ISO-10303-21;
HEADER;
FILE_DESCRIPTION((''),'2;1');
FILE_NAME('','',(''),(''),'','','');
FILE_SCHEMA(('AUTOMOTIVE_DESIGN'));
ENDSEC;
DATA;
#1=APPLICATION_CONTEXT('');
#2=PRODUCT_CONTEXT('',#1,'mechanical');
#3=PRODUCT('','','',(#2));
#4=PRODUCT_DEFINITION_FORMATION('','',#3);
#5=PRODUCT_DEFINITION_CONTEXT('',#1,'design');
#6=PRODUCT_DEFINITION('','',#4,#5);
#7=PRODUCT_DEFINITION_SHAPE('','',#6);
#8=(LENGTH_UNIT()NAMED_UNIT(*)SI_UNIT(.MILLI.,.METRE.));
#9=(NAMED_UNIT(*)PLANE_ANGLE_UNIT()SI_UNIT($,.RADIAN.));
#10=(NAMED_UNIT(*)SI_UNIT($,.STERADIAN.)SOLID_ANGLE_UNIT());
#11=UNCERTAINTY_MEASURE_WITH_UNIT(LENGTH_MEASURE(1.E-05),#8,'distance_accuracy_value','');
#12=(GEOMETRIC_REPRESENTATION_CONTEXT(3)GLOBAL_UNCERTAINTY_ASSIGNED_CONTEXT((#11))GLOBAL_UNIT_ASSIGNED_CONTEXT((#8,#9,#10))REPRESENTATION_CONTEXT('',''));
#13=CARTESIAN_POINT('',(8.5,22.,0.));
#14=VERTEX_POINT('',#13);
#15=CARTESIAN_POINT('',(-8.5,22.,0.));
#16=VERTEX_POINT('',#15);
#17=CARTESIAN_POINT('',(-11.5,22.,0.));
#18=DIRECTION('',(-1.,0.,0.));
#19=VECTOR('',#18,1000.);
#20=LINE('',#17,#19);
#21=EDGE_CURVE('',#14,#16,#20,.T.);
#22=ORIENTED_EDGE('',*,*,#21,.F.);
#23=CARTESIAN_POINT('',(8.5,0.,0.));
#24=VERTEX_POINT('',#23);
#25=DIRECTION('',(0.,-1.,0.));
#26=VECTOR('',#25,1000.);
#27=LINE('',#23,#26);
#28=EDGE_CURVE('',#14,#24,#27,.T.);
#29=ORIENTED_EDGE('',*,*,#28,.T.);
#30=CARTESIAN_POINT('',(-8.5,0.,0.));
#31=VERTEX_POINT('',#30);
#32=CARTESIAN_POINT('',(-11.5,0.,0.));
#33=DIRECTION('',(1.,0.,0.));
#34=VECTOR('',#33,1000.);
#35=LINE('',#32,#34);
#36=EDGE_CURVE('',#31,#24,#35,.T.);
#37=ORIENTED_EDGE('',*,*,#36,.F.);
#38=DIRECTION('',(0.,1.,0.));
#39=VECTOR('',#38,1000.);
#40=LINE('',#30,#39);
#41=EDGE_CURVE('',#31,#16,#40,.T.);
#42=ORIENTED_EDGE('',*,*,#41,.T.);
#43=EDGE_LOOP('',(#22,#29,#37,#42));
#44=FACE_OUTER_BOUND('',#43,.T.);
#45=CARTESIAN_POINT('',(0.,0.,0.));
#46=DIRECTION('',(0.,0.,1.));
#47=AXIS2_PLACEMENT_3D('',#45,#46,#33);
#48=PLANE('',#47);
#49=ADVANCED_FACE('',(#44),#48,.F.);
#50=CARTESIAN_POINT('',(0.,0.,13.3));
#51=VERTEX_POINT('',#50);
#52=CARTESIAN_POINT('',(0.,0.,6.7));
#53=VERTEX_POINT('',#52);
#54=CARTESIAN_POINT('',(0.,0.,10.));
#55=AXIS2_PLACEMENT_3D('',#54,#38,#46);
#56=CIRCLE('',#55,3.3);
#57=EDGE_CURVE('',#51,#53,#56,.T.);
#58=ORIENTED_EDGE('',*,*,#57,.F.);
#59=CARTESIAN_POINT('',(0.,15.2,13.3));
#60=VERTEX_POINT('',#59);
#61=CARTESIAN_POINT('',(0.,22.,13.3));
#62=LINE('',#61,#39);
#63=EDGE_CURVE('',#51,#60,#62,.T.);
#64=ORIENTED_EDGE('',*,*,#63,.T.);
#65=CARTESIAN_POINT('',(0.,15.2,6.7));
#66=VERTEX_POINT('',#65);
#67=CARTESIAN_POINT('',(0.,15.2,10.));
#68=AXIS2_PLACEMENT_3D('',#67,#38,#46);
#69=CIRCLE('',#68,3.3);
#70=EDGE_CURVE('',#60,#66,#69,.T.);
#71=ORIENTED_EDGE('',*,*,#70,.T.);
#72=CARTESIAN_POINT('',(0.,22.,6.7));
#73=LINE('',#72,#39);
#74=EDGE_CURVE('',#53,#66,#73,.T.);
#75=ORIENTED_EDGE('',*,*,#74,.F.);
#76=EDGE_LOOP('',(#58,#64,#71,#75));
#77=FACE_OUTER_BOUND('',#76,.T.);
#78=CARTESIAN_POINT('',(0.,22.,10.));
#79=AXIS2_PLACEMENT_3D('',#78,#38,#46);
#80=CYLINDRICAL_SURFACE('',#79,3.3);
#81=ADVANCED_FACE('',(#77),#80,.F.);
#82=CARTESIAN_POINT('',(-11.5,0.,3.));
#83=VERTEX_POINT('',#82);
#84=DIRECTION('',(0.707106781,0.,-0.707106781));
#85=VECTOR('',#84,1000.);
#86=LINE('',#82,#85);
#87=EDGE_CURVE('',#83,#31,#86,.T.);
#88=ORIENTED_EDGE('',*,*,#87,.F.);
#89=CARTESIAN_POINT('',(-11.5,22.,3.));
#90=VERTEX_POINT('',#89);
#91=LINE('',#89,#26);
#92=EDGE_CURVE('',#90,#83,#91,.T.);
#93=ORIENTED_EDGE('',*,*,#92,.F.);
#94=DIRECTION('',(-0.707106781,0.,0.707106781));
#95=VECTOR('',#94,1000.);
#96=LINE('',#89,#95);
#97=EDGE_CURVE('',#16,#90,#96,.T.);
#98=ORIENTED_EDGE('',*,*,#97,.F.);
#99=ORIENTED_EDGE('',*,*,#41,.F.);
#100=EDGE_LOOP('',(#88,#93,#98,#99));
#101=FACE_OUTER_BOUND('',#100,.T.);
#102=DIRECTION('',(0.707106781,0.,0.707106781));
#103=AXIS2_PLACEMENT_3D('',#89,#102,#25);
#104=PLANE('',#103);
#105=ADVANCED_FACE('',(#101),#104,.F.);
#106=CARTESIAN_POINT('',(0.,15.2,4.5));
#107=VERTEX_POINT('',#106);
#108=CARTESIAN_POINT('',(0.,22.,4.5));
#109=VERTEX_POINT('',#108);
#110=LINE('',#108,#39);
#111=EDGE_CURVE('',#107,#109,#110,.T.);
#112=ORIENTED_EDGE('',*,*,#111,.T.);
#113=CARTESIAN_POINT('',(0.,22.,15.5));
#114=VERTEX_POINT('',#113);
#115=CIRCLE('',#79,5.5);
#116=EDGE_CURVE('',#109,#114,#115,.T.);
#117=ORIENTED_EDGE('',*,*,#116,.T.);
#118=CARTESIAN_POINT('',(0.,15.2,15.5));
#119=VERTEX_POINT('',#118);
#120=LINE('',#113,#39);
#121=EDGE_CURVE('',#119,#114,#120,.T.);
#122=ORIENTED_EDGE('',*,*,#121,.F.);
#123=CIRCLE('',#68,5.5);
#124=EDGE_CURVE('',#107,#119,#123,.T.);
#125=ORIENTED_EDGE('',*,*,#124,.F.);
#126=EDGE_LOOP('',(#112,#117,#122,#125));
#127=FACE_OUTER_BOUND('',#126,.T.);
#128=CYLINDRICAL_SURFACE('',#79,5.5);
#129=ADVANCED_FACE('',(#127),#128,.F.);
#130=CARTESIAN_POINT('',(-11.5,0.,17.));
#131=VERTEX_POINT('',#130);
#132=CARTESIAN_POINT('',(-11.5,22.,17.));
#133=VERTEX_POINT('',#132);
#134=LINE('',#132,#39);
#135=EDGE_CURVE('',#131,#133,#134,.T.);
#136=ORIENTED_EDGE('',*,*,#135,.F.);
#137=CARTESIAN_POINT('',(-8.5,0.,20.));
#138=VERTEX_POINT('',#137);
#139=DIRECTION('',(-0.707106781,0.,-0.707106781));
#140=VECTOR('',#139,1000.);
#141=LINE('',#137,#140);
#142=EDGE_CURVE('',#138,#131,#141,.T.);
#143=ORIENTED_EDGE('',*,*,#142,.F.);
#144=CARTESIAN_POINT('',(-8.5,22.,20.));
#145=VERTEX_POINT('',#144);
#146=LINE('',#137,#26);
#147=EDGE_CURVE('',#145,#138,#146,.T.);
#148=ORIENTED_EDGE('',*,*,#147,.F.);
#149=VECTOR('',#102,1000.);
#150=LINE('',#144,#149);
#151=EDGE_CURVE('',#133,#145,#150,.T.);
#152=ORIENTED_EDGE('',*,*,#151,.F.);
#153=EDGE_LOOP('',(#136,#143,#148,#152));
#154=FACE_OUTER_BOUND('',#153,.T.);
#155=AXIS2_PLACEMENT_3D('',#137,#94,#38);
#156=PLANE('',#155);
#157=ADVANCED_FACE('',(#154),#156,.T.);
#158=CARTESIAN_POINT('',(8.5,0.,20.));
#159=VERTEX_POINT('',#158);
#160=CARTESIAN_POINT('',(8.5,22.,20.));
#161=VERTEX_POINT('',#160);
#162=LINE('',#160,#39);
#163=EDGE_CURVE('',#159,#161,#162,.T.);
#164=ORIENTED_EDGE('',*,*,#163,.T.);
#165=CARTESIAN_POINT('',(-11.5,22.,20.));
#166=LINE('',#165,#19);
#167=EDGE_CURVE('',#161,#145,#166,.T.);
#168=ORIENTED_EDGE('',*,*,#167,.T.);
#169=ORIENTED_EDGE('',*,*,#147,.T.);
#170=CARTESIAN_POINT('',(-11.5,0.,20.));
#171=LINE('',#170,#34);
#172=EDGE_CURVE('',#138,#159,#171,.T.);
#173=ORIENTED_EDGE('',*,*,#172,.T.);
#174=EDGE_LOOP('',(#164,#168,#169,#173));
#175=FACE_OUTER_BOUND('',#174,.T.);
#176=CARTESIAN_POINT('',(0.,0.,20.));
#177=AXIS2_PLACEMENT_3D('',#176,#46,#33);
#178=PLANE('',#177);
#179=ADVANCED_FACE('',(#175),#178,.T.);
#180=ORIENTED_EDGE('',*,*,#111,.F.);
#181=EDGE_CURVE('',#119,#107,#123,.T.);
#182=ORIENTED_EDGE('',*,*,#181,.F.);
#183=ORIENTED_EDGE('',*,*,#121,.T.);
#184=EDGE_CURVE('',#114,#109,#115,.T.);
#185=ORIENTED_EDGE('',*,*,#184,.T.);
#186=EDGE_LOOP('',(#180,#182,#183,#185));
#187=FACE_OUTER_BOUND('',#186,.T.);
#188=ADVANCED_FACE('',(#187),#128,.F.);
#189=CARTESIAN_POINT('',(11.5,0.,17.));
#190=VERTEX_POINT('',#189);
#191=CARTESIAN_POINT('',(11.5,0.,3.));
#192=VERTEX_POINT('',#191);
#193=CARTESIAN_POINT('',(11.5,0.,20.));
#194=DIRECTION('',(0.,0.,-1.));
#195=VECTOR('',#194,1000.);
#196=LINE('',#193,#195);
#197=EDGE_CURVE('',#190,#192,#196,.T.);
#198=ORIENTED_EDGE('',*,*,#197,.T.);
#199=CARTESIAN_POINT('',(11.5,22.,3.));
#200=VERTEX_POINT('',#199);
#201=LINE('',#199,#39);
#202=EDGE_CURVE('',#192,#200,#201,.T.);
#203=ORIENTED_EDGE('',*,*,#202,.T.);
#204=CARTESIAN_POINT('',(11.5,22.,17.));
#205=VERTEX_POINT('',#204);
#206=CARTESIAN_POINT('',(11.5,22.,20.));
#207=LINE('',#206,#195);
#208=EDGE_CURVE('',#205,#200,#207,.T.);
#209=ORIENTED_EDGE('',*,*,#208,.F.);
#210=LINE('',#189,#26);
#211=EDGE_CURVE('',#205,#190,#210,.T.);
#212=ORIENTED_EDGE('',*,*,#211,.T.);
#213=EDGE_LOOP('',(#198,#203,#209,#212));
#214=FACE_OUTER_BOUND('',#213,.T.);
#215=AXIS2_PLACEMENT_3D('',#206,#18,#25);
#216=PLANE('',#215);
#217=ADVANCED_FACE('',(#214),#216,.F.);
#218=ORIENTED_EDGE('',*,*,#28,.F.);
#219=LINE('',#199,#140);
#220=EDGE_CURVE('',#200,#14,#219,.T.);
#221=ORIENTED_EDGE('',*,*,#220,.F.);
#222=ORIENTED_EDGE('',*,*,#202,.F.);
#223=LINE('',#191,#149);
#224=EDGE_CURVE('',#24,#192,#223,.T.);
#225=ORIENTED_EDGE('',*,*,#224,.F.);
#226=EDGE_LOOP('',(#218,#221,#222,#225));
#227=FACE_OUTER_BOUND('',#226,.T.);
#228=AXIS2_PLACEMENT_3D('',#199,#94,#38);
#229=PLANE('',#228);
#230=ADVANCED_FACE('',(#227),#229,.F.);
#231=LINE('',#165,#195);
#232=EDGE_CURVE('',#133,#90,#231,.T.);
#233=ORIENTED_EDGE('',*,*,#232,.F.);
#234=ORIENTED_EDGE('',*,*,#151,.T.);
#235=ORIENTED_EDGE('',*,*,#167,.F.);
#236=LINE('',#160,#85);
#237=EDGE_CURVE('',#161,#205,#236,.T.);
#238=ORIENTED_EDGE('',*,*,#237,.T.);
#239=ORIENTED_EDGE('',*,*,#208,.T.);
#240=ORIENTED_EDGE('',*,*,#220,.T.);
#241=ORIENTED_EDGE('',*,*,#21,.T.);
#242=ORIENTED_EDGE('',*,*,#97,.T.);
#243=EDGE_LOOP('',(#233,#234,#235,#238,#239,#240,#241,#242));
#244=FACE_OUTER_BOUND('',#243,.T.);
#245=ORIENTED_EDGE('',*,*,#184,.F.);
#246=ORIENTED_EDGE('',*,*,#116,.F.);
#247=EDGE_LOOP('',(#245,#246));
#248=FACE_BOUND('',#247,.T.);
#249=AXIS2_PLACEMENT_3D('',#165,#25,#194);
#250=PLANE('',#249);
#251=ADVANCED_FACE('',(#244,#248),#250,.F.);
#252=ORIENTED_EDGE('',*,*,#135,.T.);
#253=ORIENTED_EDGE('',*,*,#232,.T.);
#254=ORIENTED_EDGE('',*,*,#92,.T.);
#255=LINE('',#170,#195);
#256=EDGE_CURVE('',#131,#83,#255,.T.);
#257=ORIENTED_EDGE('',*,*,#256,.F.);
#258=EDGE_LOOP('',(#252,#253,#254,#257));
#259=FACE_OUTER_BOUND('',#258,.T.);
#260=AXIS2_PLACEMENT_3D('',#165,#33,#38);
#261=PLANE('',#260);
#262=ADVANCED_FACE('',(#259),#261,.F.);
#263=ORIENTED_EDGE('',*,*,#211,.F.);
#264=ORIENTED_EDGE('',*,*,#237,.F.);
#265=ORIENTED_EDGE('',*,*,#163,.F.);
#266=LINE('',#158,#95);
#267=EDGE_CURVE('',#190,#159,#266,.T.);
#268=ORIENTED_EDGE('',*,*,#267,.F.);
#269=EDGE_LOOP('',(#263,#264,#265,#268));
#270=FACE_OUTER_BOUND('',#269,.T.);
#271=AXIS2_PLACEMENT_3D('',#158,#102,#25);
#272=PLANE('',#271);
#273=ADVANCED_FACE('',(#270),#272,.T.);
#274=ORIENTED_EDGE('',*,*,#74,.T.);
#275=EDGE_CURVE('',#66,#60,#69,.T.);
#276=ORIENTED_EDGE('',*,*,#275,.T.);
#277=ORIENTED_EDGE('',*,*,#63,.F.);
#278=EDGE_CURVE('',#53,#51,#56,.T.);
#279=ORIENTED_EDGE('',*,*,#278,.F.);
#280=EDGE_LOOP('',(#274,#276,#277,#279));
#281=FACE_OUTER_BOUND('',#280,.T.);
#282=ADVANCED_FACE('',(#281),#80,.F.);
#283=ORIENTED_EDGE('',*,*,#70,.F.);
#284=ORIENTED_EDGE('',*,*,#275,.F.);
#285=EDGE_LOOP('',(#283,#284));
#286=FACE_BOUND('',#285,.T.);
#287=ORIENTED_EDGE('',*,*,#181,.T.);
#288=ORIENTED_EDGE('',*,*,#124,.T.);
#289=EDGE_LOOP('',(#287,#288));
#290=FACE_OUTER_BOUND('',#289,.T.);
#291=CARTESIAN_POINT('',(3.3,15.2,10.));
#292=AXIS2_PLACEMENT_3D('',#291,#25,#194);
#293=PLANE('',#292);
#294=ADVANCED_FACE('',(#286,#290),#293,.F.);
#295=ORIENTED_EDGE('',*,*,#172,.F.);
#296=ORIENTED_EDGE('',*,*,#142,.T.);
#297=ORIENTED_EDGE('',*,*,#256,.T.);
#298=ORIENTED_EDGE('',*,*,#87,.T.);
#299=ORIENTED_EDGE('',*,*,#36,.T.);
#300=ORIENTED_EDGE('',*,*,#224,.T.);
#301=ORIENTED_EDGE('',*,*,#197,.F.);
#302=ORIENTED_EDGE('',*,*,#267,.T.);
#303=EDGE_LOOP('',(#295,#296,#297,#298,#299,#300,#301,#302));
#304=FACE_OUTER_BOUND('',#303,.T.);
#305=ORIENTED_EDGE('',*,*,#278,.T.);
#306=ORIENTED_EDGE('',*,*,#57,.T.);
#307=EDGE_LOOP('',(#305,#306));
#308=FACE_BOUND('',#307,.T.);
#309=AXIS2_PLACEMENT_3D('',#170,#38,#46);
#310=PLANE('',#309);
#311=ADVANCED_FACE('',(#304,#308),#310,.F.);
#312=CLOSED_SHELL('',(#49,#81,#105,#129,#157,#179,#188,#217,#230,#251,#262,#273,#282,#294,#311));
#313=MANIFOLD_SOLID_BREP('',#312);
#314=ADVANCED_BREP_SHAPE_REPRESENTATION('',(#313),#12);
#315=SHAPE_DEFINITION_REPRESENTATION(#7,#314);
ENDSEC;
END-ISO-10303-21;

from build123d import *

# Parameters (mm, degrees)
SKETCH_1_W                = 23
SKETCH_1_H                = 22
EXTRUDE_1_DEPTH           = 20
HOLE_WIZARD_1_D           = 6.6
HOLE_WIZARD_1_CBORE_D     = 11
HOLE_WIZARD_1_CBORE_DEPTH = 6.8
CHAMFER_1_SIZE            = 3


with BuildPart() as part:
    # 草图1 → 凸台-拉伸1 (new body)
    with BuildSketch(Plane.XY):
        with Locations((0, 11)):
            Rectangle(SKETCH_1_W, SKETCH_1_H)
    extrude(amount=EXTRUDE_1_DEPTH)

    # 打孔尺寸(%根据)内六角圆柱头螺钉的类型1 (through all)
    with Locations(Plane(origin=(0, 22, 0), x_dir=(1, 0, 0), z_dir=(0, 1, 0))):
        with Locations((0, -10)):
            CounterBoreHole(HOLE_WIZARD_1_D / 2, HOLE_WIZARD_1_CBORE_D / 2, HOLE_WIZARD_1_CBORE_DEPTH)

    # 倒角1
    chamfer_1_edges = [part.edges().sort_by_distance(p)[0] for p in [
        (11.5, 11, 20),
        (-11.5, 11, 20),
        (11.5, 11, 0),
        (-11.5, 11, 0),
    ]]
    chamfer(chamfer_1_edges, length=CHAMFER_1_SIZE)


solid = part.part
